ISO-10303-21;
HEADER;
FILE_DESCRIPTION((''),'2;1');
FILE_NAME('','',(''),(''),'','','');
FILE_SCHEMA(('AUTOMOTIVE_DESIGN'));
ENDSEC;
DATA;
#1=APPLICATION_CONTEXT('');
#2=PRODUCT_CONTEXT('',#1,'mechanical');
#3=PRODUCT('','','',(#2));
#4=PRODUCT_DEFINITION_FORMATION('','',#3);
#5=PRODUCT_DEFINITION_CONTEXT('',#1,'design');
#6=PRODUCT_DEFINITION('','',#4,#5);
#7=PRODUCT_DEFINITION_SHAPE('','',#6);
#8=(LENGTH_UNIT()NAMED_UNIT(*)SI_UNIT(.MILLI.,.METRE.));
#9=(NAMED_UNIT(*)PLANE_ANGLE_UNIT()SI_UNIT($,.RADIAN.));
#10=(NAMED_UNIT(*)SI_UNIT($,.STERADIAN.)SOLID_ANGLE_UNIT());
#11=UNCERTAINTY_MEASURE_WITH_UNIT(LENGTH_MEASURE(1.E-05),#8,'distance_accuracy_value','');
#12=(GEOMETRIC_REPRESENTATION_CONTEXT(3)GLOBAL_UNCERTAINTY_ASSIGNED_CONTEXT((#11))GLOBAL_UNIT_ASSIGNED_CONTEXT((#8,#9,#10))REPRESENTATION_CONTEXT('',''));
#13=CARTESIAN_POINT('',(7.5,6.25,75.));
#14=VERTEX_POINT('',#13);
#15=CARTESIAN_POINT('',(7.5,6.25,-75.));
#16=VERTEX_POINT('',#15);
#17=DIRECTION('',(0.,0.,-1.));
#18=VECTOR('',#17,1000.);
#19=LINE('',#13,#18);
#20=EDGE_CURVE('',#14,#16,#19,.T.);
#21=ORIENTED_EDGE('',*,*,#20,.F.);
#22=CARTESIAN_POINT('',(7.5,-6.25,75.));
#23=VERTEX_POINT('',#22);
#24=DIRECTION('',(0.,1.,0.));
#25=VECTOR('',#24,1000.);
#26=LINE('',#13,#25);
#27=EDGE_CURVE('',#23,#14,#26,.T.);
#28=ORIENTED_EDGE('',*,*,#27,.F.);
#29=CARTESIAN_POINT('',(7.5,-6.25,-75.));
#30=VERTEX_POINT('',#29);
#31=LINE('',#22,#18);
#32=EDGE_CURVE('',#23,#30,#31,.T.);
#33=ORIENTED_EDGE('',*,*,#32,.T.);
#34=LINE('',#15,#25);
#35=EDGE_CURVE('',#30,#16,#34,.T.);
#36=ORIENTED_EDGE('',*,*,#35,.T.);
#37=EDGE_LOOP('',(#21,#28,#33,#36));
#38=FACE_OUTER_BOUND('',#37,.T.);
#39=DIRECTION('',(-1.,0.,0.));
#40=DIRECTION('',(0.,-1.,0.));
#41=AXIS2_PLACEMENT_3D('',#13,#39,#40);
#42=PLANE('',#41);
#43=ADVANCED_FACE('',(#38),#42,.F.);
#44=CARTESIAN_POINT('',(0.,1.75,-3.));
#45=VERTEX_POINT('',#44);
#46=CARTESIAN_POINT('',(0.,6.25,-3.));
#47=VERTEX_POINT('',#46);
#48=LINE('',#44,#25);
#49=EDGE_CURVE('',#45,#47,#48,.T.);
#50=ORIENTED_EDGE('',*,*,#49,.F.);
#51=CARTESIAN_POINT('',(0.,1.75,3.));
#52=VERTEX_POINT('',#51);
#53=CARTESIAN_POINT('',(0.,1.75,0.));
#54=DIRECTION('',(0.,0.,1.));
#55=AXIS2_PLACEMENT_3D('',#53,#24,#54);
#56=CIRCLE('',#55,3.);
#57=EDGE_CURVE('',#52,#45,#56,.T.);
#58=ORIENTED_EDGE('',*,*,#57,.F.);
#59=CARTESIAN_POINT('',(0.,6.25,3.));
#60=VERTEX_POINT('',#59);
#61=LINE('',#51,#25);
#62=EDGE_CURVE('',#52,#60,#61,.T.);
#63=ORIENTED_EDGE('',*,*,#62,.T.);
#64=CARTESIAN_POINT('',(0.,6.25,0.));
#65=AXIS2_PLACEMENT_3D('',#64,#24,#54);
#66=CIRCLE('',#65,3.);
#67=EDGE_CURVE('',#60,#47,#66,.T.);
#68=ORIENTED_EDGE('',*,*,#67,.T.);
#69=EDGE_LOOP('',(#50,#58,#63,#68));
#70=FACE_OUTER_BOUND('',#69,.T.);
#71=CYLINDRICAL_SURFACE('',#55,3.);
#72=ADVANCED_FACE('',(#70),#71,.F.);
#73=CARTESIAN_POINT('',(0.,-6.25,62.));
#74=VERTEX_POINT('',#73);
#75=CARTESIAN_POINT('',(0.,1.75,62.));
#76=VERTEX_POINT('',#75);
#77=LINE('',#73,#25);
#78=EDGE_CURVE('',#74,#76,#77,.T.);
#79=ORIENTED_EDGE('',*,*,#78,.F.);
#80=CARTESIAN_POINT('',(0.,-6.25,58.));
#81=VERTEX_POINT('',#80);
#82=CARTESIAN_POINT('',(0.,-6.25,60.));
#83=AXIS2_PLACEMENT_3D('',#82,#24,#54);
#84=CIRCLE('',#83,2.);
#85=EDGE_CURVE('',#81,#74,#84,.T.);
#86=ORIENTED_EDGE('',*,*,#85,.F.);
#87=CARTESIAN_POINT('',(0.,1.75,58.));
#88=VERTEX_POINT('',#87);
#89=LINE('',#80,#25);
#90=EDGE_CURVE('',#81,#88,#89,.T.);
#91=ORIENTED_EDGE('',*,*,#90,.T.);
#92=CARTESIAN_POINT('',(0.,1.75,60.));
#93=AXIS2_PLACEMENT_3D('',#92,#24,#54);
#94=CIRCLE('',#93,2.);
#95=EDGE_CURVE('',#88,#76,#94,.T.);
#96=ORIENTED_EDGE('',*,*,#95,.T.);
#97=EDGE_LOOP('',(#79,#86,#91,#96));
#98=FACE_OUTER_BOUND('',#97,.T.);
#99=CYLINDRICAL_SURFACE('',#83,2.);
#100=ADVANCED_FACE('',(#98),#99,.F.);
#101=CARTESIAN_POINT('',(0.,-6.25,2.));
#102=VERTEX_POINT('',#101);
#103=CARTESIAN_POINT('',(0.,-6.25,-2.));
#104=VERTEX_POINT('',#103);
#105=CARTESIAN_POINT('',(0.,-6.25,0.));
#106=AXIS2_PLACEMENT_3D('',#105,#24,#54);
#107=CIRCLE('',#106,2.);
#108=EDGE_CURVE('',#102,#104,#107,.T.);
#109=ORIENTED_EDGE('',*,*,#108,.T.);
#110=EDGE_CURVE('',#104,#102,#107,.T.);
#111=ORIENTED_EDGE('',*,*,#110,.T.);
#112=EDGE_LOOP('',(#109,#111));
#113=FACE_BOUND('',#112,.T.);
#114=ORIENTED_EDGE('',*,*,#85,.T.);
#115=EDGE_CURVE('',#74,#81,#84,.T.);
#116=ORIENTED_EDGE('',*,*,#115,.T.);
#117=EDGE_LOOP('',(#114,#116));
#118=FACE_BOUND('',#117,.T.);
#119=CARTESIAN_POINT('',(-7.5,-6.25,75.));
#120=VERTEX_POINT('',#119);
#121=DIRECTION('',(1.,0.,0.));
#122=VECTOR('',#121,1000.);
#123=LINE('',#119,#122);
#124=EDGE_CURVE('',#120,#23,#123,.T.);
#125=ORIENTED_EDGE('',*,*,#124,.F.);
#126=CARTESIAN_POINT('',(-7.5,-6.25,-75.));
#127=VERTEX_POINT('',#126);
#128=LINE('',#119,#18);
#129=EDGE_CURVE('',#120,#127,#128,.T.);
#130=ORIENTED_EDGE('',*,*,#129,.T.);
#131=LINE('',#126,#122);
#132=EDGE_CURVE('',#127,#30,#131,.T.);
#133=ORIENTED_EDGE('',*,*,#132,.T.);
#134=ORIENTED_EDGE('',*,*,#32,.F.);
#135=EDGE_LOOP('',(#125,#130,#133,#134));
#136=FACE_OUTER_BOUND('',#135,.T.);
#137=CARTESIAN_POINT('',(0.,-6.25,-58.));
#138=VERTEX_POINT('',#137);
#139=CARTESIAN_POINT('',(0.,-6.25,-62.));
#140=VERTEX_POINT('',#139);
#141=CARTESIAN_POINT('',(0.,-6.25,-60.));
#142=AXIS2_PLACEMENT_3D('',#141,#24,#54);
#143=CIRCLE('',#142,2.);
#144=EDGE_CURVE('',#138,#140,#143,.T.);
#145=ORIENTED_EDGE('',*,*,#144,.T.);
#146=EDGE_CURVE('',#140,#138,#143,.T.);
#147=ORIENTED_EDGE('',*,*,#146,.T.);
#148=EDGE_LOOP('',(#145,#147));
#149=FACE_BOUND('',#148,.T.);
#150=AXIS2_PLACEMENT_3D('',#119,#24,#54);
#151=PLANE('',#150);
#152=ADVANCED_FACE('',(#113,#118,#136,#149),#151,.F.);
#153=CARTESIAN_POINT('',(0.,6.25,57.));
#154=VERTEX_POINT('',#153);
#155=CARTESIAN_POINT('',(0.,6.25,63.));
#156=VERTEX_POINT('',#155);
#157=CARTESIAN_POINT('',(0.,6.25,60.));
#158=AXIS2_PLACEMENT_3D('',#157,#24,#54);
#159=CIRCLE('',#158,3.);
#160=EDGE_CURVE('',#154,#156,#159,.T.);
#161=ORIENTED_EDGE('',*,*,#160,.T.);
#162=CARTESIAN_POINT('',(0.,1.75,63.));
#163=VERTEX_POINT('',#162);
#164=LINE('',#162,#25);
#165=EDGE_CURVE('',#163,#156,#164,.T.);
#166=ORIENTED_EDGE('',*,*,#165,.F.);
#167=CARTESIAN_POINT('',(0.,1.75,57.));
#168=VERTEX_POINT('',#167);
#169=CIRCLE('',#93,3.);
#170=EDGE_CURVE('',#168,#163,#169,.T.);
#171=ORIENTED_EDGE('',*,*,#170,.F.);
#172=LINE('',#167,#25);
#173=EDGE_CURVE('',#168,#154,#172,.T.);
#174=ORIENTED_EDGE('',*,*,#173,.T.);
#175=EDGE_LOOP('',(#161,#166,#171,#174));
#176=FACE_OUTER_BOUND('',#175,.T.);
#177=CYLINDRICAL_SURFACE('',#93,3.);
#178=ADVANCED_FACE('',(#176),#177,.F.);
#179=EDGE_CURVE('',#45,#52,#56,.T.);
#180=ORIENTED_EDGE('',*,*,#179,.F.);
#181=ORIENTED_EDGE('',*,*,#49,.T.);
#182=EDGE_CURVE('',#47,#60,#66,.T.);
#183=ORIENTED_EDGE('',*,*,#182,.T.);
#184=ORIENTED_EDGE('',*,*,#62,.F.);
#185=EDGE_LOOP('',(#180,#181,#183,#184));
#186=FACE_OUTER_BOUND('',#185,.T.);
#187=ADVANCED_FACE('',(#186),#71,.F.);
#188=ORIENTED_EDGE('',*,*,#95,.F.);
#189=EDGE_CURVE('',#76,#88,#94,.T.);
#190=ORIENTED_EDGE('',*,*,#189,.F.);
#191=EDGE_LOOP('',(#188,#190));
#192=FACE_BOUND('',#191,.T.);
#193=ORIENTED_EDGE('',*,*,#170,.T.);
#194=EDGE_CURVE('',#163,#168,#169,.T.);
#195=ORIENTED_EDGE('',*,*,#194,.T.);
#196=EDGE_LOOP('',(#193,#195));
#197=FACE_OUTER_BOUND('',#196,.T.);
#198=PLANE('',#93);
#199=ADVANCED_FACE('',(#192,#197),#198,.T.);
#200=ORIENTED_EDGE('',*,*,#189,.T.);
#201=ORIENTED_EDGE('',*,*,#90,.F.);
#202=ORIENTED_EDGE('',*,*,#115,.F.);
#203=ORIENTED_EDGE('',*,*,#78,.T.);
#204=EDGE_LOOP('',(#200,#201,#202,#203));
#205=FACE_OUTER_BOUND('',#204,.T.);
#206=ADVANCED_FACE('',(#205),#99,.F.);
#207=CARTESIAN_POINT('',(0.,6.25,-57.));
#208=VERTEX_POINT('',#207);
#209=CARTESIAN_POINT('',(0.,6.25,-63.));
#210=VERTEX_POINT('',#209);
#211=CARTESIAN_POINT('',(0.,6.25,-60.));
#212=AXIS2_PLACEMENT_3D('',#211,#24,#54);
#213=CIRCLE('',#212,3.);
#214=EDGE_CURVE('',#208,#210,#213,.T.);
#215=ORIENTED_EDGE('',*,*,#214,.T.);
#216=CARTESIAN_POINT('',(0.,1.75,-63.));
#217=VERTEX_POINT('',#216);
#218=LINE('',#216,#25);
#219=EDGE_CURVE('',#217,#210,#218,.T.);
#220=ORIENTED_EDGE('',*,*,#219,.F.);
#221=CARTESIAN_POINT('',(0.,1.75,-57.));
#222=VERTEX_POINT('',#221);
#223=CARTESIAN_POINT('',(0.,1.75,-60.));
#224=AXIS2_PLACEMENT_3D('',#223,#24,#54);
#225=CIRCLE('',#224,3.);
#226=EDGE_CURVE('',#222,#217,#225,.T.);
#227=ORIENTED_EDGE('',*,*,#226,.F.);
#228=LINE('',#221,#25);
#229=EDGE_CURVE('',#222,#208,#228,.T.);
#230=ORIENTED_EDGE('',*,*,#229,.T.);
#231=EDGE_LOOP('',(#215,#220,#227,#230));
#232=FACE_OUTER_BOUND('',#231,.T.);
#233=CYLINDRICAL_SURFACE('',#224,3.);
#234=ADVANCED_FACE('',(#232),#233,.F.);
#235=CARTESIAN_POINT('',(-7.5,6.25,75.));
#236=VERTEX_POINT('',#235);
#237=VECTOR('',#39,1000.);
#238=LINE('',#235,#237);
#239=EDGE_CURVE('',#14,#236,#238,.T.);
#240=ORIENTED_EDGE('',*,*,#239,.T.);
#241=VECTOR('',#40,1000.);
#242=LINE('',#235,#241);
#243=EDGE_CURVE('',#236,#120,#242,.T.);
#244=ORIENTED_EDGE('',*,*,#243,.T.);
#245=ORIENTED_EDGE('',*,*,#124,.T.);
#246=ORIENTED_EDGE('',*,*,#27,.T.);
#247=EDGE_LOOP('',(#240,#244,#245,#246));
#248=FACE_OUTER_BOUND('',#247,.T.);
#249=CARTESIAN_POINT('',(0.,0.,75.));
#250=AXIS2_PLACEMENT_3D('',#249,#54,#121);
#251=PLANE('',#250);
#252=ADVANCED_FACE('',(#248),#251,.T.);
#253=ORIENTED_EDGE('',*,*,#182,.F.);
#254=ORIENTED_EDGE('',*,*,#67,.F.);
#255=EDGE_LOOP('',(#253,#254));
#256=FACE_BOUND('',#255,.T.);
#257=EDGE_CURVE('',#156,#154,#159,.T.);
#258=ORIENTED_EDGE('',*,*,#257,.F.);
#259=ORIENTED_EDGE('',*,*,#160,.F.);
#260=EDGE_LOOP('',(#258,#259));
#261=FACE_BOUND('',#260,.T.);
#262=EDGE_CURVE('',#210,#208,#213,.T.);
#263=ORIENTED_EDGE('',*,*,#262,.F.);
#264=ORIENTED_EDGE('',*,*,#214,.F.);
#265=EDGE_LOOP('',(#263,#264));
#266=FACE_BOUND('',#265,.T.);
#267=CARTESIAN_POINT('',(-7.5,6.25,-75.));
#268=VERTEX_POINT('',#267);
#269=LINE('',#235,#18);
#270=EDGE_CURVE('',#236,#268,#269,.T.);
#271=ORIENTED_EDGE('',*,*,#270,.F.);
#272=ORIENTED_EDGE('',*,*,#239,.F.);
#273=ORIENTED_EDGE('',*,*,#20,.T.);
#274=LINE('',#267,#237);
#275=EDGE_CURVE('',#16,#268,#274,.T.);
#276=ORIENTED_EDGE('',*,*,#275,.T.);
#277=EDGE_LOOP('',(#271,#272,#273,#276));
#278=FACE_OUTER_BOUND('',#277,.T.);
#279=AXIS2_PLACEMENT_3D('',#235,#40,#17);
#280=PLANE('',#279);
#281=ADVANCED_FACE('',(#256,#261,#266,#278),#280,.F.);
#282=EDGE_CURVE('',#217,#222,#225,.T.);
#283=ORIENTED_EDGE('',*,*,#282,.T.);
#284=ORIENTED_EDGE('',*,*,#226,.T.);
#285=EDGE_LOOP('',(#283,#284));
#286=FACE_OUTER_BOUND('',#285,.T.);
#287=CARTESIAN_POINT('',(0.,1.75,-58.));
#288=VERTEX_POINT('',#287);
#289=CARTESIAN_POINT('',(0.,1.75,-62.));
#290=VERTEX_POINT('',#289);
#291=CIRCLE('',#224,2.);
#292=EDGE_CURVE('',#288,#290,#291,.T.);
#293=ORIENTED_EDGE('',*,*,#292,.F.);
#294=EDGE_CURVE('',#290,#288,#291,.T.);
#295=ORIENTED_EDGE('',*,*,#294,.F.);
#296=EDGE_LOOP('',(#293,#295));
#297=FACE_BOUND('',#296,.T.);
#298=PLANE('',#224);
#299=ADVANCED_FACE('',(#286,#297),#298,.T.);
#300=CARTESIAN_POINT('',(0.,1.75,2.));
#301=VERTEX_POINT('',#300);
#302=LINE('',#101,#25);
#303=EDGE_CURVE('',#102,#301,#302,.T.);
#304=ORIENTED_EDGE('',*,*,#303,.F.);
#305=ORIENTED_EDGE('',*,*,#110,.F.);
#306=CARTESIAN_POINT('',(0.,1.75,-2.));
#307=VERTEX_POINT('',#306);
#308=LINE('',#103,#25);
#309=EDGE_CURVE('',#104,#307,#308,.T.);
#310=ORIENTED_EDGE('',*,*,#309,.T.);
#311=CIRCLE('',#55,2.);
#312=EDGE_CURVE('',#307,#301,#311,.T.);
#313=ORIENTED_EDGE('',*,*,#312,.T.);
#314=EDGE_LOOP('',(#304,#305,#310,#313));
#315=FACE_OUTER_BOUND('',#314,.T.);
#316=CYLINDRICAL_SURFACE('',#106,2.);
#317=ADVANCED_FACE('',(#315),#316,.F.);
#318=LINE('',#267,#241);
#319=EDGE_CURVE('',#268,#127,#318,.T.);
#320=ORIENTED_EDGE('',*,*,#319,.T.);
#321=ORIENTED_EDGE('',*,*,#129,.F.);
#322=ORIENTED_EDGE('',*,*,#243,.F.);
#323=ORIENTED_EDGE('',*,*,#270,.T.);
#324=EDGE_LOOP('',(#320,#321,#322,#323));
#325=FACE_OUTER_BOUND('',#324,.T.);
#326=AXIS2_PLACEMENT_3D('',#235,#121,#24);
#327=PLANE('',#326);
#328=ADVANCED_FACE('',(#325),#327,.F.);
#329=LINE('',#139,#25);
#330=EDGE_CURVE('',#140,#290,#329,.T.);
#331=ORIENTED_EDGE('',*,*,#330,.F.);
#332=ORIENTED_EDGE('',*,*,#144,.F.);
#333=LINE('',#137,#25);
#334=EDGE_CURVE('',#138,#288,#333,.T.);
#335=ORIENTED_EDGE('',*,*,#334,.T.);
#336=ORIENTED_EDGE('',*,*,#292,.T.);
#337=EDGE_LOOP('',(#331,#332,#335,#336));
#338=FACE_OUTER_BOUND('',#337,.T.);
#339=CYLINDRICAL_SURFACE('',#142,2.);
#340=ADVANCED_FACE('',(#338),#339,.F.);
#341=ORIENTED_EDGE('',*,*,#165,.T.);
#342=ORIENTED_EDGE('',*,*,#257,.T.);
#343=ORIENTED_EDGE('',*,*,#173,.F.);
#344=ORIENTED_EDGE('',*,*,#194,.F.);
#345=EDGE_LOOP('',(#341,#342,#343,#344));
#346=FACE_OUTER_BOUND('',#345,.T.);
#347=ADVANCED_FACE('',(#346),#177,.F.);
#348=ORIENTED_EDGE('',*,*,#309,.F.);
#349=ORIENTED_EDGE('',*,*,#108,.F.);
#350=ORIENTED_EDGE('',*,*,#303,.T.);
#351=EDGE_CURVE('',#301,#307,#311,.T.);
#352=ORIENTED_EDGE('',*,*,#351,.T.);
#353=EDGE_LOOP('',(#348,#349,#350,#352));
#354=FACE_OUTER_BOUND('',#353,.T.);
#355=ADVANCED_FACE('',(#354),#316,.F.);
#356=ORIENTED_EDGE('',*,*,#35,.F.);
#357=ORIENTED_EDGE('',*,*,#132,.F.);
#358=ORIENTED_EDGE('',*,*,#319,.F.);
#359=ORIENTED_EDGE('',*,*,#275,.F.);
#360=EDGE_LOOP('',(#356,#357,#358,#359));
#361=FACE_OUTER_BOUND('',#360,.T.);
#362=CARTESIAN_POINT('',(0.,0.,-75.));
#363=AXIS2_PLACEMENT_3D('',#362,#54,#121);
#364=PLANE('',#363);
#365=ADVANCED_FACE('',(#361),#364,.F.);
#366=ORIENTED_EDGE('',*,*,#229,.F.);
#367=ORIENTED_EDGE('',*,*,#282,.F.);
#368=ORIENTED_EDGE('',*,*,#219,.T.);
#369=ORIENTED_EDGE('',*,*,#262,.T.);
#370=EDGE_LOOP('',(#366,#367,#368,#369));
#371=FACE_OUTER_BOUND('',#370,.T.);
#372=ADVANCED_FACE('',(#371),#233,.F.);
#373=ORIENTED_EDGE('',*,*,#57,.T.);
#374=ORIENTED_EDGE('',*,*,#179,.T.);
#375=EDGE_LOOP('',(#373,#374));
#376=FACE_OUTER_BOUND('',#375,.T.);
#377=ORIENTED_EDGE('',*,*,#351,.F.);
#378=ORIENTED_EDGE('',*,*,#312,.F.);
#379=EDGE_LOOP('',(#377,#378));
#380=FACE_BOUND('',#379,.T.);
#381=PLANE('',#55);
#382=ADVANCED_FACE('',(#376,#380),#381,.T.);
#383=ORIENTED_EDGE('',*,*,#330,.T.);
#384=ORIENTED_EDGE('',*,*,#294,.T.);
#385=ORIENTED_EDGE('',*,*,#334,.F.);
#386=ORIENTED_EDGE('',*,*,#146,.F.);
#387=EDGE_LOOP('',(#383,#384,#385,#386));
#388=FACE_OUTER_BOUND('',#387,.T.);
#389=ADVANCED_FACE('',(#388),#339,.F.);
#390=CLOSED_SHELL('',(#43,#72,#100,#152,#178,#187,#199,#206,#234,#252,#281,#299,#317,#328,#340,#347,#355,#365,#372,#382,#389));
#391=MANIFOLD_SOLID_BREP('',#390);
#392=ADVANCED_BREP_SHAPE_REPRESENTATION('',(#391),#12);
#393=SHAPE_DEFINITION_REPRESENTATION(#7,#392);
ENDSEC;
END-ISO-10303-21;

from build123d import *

# Parameters (mm, degrees)
SKETCH_1_W             = 15
SKETCH_1_H             = 12.5
EXTRUDE_1_DEPTH        = 75
SKETCH_2_R             = 3
CUT_EXTRUDE_1_DEPTH    = 4.5
SKETCH_3_R             = 2
CUT_EXTRUDE_2_DEPTH    = 77.40353395
PATTERN_LINEAR_1_COUNT = 6
PATTERN_LINEAR_1_PITCH = 60


with BuildPart() as part:
    # 草图1 → 凸台-拉伸1 (new, symmetric)
    with BuildSketch(Plane.XY):
        Rectangle(SKETCH_1_W, SKETCH_1_H)
    extrude(amount=EXTRUDE_1_DEPTH, both=True)

    # 草图2 → 切除-拉伸1 (cut)
    with BuildSketch(Plane(origin=(0, 6.25, 0), x_dir=(1, 0, 0), z_dir=(0, 1, 0))):
        with Locations(Location((0, -60, 0), (0, 0, 270))):
            Circle(SKETCH_2_R)
    cut_extrude_1 = extrude(amount=-CUT_EXTRUDE_1_DEPTH, mode=Mode.SUBTRACT)

    # 草图3 → 切除-拉伸2 (cut, through all)
    with BuildSketch(Plane(origin=(0, 6.25, 0), x_dir=(1, 0, 0), z_dir=(0, 1, 0))):
        with Locations(Location((0, -60, 0), (0, 0, 270))):
            Circle(SKETCH_3_R)
    cut_extrude_2 = extrude(amount=-CUT_EXTRUDE_2_DEPTH, mode=Mode.SUBTRACT)

    # 阵列(线性)1: 切除-拉伸1, 切除-拉伸2 ×6
    with Locations(*[(0, 0, -i * PATTERN_LINEAR_1_PITCH) for i in range(1, PATTERN_LINEAR_1_COUNT)]):
        add(cut_extrude_1, mode=Mode.SUBTRACT)
        add(cut_extrude_2, mode=Mode.SUBTRACT)


solid = part.part
